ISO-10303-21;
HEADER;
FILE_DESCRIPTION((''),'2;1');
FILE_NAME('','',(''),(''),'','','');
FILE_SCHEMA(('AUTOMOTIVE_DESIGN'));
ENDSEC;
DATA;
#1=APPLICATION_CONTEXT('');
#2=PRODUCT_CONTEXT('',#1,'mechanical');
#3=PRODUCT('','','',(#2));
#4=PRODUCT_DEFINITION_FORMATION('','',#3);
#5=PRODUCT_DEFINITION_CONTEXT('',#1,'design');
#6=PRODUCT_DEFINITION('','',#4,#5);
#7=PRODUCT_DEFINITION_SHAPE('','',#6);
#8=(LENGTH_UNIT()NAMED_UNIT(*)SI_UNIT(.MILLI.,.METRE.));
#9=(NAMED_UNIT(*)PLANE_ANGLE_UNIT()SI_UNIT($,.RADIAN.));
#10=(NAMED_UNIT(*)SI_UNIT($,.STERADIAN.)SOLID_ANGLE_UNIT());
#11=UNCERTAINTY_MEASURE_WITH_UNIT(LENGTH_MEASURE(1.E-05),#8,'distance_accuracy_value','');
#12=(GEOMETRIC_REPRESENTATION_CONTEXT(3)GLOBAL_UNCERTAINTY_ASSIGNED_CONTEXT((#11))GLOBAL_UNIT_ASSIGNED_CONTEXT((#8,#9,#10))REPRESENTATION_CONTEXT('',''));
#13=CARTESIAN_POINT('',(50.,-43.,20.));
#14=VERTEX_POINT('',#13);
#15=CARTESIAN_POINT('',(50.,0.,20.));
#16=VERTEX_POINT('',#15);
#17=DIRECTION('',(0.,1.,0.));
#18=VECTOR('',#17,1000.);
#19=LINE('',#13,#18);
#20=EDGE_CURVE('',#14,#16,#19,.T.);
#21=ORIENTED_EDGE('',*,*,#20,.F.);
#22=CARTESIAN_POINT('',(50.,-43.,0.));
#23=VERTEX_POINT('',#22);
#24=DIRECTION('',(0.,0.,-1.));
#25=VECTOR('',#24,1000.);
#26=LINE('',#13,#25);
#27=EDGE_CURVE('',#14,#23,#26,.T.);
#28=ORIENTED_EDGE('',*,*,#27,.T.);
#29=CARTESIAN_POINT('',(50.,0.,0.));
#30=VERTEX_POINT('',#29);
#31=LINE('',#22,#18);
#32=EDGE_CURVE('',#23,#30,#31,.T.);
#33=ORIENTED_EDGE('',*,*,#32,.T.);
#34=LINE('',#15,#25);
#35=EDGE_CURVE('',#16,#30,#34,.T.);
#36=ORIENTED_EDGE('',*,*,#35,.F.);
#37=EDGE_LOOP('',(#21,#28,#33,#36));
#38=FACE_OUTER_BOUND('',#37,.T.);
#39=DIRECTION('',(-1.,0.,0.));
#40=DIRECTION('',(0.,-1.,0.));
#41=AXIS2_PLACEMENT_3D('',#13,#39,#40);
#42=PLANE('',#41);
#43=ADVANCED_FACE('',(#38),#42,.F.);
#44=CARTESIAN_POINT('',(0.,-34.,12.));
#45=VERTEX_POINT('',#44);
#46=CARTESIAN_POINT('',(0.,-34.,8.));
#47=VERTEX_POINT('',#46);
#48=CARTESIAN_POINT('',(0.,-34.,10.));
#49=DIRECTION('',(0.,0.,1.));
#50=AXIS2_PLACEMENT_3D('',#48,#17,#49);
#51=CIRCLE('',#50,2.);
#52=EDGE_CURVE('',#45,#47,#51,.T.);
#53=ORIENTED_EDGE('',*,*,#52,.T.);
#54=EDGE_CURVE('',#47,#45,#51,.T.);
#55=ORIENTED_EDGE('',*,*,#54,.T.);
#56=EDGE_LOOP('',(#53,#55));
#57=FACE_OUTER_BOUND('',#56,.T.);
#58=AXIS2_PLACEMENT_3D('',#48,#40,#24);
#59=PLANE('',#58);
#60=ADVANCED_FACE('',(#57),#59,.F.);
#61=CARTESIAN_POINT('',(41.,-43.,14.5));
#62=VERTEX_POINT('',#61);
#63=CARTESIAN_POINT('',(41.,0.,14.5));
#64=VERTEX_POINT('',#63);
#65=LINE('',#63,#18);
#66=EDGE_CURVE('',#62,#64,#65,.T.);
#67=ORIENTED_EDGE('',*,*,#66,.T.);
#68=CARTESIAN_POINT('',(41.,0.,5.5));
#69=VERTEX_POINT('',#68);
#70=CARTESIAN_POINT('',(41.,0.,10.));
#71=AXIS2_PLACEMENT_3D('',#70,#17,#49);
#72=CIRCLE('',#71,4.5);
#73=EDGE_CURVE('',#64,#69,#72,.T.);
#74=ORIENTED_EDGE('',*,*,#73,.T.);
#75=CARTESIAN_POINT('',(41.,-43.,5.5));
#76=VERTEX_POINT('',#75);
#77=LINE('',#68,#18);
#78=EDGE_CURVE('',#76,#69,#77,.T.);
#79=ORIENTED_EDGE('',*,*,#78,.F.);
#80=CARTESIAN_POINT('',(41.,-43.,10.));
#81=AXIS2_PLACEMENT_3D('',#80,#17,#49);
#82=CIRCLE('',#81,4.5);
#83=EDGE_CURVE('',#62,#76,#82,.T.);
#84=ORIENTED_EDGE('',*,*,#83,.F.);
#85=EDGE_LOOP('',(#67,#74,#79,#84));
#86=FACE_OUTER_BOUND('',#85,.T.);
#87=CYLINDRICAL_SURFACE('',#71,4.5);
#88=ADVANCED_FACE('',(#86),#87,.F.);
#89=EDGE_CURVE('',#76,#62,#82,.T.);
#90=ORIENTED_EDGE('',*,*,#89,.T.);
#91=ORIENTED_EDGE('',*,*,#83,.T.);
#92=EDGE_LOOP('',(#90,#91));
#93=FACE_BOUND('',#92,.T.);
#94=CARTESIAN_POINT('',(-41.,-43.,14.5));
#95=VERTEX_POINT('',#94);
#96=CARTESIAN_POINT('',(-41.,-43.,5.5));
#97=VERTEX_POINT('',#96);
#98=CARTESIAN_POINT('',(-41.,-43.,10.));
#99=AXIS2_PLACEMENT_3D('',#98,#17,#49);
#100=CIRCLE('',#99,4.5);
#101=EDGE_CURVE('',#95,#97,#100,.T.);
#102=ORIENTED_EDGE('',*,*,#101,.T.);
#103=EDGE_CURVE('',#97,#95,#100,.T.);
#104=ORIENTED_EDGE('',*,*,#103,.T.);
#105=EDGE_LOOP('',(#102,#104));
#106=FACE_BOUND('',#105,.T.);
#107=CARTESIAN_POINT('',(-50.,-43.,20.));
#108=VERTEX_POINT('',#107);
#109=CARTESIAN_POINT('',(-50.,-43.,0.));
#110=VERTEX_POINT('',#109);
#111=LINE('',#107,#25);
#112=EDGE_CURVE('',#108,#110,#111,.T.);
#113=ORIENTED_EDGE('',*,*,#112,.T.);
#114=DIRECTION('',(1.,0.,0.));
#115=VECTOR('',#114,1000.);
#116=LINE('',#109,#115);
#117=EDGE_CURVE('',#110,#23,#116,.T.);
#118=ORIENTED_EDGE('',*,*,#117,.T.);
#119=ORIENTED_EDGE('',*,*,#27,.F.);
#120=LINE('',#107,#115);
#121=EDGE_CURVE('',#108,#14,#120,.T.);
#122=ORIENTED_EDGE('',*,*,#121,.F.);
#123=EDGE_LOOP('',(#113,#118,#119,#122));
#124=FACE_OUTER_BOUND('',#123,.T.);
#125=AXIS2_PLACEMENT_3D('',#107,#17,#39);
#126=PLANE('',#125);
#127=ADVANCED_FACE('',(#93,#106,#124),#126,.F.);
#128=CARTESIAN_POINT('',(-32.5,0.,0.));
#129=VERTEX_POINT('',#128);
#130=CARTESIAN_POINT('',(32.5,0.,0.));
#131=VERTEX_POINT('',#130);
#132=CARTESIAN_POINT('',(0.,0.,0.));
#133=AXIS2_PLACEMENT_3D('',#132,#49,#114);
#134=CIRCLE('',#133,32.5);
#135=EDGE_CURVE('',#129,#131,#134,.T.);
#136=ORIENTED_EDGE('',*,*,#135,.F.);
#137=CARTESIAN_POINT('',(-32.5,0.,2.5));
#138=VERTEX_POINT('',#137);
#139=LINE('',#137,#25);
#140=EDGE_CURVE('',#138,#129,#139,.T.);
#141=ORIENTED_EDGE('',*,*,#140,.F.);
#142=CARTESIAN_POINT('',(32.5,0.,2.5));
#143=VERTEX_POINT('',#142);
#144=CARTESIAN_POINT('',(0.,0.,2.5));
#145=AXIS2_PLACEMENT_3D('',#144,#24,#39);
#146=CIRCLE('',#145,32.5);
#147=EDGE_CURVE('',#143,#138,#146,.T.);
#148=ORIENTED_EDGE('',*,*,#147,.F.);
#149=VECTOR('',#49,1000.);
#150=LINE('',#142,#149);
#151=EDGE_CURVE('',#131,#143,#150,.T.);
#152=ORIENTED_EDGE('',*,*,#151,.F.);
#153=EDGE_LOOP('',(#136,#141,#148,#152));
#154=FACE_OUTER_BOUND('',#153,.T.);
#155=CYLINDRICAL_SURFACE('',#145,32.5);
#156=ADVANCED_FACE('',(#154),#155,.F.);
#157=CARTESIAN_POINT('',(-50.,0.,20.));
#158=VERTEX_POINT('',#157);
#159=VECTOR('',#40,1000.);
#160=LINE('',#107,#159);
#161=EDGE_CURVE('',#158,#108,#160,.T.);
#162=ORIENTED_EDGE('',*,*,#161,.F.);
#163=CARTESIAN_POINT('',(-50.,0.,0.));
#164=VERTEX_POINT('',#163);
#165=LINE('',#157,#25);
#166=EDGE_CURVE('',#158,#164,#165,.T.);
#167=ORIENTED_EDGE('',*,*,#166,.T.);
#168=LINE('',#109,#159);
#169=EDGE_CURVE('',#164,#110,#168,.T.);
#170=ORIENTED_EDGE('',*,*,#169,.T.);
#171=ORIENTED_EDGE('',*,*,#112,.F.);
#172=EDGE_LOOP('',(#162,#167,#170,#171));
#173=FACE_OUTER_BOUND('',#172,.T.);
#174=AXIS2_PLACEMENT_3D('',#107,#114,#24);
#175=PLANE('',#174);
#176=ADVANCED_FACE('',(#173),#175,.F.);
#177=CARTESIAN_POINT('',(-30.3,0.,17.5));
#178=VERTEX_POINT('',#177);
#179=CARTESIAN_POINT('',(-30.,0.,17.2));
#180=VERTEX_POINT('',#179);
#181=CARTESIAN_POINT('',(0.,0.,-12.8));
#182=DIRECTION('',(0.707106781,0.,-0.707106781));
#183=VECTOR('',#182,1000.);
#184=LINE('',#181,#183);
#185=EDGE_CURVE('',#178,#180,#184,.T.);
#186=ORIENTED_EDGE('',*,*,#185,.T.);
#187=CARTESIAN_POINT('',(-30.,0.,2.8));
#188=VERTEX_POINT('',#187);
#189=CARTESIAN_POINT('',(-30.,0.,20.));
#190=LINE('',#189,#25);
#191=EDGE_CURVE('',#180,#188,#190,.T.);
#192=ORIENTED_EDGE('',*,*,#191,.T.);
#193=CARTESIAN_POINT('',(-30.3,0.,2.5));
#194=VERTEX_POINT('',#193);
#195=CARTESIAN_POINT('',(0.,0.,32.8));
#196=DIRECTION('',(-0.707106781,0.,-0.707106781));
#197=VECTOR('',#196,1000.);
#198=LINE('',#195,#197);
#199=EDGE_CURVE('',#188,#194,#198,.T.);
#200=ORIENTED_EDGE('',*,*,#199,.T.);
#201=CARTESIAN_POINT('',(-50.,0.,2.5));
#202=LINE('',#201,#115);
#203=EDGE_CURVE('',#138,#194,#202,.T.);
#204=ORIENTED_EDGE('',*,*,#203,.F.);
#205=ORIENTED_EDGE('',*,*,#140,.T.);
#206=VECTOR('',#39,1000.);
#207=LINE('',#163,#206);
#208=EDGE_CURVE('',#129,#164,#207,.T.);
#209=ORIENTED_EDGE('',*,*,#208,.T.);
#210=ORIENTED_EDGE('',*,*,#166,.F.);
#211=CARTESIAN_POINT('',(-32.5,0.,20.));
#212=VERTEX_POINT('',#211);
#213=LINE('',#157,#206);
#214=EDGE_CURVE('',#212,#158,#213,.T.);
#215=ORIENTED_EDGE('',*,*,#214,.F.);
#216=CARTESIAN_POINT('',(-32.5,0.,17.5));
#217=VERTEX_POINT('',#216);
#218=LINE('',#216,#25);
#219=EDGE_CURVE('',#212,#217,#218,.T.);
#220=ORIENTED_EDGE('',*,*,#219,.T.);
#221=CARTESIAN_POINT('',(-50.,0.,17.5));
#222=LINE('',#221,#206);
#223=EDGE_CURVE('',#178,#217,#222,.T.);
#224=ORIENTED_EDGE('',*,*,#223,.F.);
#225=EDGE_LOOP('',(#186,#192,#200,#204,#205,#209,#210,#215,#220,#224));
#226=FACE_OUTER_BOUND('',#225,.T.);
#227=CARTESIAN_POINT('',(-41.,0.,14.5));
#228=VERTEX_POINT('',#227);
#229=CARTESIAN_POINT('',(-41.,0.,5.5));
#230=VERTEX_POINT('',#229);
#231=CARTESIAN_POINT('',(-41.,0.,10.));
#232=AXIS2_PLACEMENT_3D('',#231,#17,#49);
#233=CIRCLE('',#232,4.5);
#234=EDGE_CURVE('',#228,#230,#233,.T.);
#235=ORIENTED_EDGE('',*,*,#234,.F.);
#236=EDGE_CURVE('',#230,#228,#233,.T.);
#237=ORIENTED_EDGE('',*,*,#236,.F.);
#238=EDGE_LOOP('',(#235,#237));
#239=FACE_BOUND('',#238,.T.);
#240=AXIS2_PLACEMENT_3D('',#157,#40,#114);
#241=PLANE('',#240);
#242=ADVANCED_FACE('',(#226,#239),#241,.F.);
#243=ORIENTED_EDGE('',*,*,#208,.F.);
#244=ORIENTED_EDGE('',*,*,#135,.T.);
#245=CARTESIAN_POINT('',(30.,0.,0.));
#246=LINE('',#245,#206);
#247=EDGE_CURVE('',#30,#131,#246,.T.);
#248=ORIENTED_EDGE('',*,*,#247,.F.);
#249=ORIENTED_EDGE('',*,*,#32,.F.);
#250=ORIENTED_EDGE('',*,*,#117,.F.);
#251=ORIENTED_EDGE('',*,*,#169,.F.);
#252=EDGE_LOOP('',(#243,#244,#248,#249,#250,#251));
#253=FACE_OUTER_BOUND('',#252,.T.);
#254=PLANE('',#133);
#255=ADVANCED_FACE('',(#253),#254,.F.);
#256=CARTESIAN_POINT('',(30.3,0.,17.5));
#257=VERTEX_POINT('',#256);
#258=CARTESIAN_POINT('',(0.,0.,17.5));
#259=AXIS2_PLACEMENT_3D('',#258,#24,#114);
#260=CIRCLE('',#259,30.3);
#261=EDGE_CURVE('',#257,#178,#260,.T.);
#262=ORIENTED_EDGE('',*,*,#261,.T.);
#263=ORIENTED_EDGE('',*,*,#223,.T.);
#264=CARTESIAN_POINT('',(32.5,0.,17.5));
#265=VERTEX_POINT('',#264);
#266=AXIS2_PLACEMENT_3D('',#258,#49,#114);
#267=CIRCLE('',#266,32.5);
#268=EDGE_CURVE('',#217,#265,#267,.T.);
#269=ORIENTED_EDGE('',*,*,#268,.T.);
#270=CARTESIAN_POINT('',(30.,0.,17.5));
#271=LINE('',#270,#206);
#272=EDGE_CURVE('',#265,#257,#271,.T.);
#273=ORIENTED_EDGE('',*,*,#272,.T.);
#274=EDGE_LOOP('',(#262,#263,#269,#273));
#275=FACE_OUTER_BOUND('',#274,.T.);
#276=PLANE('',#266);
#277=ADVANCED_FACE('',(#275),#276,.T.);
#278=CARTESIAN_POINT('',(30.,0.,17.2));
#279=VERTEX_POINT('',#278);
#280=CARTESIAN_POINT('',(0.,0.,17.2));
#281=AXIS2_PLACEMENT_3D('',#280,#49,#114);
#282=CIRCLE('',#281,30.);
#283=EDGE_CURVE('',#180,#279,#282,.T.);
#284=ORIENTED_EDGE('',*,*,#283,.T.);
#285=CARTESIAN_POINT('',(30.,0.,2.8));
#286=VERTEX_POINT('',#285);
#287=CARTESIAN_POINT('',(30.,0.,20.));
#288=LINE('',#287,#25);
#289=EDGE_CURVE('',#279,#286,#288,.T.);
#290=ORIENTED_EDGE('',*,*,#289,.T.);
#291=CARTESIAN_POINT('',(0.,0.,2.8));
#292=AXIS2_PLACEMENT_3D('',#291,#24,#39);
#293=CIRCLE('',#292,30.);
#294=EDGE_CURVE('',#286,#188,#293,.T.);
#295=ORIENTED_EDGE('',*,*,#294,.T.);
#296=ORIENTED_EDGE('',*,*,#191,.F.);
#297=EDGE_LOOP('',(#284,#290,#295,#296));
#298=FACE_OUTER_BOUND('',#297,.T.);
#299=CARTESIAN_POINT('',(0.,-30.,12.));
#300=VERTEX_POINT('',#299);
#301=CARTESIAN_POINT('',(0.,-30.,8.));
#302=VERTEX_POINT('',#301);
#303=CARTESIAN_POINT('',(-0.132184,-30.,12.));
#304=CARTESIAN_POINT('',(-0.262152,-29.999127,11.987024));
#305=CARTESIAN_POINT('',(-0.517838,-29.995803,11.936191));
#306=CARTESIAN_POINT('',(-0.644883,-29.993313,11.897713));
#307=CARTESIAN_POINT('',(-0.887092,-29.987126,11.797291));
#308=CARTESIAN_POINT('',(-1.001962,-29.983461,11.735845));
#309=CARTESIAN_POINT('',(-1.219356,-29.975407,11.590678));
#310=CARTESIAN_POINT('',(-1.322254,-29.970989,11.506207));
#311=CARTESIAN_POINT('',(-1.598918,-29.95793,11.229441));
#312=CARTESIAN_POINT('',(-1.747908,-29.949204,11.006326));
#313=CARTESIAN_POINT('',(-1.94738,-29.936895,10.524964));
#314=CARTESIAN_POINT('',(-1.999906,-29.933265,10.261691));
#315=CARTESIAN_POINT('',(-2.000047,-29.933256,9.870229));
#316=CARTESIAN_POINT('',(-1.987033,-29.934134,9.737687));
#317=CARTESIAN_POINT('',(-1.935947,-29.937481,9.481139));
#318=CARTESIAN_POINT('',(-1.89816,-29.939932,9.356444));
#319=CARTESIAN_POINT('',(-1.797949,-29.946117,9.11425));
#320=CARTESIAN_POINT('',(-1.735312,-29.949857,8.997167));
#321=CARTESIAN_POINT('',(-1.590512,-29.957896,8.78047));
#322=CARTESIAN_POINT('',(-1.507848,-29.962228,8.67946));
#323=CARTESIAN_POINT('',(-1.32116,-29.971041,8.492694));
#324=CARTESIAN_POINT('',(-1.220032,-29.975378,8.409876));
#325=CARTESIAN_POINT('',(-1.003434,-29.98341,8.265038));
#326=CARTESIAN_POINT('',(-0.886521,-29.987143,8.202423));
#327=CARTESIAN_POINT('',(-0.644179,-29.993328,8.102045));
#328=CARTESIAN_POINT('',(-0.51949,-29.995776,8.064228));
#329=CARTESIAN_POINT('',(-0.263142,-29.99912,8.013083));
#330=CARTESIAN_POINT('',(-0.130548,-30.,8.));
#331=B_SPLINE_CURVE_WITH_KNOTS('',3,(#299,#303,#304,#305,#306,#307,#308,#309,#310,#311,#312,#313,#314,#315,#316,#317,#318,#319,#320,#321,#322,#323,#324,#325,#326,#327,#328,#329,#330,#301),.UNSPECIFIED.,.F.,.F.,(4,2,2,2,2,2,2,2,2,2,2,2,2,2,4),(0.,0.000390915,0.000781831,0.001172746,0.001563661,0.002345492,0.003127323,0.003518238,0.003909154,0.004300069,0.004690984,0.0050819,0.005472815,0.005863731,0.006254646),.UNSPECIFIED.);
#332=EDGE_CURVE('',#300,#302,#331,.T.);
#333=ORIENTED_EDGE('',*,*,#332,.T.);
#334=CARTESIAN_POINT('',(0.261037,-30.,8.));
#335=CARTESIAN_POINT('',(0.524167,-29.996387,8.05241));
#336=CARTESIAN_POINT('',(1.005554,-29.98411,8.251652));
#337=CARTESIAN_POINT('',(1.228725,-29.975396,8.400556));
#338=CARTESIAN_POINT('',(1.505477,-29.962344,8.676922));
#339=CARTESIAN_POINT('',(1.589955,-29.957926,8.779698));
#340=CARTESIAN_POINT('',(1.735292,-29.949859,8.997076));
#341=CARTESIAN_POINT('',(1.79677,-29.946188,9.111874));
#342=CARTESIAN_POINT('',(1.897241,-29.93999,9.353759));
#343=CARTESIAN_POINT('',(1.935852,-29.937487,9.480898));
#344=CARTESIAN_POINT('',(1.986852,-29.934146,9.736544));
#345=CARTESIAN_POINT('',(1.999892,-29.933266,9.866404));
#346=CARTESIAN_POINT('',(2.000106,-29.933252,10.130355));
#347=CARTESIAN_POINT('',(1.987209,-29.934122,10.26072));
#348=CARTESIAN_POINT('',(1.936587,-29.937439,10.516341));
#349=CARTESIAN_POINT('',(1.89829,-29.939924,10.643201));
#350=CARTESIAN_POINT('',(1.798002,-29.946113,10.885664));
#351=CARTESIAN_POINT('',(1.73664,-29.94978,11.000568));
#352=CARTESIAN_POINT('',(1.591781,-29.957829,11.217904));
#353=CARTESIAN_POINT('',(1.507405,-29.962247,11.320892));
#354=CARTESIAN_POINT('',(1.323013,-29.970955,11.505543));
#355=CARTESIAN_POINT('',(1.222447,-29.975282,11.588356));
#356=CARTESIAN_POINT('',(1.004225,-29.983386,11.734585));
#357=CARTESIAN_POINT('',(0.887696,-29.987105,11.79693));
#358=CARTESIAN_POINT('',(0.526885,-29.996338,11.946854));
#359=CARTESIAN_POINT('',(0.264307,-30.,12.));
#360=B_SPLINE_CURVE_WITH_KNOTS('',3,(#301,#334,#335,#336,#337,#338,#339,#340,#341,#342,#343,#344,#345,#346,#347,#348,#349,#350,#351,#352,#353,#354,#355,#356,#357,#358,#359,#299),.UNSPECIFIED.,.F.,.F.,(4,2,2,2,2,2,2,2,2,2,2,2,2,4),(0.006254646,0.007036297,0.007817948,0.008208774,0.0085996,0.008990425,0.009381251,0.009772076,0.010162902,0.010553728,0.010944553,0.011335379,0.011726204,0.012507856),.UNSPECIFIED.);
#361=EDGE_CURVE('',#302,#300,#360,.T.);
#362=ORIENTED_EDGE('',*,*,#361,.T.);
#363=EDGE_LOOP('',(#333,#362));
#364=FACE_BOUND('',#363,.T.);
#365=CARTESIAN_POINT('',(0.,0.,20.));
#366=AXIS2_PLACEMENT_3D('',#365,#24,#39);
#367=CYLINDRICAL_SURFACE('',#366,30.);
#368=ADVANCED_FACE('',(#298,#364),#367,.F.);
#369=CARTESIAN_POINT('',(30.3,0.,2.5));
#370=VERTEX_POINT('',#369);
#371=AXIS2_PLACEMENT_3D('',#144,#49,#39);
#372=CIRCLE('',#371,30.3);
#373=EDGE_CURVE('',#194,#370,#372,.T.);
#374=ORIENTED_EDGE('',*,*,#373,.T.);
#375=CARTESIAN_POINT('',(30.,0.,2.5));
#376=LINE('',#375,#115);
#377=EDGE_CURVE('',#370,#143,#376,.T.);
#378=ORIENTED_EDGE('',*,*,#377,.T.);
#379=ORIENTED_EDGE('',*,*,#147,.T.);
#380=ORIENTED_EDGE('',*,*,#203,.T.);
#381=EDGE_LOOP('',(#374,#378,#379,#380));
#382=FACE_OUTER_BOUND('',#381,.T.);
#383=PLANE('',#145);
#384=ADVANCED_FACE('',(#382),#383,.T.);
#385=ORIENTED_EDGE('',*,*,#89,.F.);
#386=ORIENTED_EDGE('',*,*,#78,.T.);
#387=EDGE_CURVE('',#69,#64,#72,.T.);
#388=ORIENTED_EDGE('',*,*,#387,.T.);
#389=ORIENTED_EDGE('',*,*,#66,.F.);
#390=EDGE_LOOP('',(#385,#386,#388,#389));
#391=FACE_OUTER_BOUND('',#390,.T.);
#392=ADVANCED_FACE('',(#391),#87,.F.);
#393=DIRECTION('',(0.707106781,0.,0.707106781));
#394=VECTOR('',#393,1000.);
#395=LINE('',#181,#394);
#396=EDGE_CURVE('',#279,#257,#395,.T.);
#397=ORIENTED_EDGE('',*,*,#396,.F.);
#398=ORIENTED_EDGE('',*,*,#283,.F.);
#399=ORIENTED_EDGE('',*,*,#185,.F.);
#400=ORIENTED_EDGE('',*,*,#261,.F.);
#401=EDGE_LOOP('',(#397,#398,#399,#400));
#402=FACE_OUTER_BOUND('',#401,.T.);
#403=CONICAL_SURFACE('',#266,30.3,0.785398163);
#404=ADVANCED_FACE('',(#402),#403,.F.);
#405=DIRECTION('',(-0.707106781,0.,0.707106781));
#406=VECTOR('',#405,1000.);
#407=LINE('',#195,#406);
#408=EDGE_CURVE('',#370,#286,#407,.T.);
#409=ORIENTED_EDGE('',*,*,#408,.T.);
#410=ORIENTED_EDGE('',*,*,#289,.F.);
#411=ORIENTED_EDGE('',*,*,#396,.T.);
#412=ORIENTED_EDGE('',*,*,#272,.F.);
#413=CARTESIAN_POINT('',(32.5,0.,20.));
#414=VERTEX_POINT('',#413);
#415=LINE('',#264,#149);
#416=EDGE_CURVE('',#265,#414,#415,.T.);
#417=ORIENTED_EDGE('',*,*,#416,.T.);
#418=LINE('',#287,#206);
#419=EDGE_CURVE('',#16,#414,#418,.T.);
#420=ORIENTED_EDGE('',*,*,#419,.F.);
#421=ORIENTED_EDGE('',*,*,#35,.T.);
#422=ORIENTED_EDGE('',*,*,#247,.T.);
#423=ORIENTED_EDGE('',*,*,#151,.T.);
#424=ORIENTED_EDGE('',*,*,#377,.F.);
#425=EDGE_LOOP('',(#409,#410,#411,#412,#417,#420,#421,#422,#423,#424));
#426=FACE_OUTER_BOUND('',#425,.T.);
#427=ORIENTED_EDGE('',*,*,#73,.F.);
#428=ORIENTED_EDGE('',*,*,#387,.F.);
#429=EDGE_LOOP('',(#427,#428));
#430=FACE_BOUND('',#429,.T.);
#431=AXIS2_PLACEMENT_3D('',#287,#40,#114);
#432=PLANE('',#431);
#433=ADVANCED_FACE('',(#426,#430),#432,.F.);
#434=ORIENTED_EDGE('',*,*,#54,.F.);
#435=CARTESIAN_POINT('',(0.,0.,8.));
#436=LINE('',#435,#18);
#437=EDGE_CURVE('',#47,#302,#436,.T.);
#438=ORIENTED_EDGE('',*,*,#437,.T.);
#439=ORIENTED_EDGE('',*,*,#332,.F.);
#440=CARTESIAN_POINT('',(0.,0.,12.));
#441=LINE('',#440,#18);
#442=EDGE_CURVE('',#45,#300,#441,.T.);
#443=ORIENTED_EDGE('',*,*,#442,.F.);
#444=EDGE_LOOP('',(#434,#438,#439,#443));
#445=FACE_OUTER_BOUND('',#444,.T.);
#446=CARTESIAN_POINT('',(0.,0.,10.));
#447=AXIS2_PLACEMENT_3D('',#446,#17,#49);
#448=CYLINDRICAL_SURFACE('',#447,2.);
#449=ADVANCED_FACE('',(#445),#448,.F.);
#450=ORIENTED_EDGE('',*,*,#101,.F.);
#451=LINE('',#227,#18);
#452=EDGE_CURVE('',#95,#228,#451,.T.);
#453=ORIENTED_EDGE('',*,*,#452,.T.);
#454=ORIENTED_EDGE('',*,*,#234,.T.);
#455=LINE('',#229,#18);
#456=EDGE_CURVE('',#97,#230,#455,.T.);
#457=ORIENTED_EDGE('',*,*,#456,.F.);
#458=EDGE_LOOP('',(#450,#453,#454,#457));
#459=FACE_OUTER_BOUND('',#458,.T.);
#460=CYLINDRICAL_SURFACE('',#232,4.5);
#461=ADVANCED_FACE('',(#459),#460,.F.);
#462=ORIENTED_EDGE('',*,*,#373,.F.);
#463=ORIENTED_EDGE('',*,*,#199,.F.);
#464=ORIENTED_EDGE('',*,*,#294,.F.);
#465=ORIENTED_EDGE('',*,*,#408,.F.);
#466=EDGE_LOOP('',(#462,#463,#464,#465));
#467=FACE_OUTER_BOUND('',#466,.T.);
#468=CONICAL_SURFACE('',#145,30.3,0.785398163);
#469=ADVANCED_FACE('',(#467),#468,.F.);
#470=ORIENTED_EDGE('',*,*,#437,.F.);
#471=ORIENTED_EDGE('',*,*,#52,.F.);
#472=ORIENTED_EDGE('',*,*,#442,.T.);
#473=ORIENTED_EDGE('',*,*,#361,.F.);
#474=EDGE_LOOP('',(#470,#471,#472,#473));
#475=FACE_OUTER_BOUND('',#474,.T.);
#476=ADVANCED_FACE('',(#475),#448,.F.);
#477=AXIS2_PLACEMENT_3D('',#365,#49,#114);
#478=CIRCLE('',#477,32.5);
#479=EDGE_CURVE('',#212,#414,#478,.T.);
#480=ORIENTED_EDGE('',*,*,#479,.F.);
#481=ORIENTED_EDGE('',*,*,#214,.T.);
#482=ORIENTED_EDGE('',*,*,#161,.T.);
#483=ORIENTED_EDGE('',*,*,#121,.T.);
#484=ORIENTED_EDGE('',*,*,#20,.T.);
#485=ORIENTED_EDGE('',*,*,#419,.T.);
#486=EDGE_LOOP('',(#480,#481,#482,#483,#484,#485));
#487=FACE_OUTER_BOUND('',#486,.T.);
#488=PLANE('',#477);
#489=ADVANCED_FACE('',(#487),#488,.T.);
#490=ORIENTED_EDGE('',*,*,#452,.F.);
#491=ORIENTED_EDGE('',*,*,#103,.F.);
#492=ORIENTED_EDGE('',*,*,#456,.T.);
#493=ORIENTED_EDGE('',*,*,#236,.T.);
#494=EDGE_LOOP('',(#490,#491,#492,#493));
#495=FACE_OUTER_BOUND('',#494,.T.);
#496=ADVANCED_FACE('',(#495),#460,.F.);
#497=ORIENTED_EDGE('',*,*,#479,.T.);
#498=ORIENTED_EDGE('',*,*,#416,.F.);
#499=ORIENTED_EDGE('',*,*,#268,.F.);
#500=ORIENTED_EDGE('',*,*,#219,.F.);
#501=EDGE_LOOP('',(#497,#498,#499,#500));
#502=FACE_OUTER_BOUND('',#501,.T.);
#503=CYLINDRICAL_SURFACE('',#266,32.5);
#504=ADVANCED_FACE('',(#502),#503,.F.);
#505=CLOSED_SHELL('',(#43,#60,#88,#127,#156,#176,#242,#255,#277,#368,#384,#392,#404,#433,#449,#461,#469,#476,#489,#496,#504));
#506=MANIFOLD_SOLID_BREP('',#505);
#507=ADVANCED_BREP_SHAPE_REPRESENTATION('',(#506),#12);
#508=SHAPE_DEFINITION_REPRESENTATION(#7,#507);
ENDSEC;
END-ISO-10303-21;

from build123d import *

# Parameters (mm, degrees)
BOSS_EXTRUDE1_DEPTH = 20
SKETCH2_R           = 32.5
CUT_EXTRUDE1_DEPTH  = 2.5
CUT_EXTRUDE2_START  = -2.5
SKETCH3_R           = 32.5
CUT_EXTRUDE2_DEPTH  = 2.5
CHAMFER1_SIZE       = 0.3
HOLE1_D             = 9
HOLE2_D             = 4
HOLE2_DEPTH         = 34


with BuildPart() as part:
    # Sketch1 → Boss-Extrude1 (new body)
    with BuildSketch(Plane.XY):
        with BuildLine():
            Line((-50, 0), (-30, 0))
            ThreePointArc((-30, 0), (0, -30), (30, 0))
            Line((30, 0), (50, 0))
            Line((50, 0), (50, -43))
            Line((50, -43), (-50, -43))
            Line((-50, -43), (-50, 0))
        make_face()
    extrude(amount=BOSS_EXTRUDE1_DEPTH)

    # Sketch2 → Cut-Extrude1 (cut)
    with BuildSketch(Plane.XY.offset(20)):
        Circle(SKETCH2_R)
    extrude(amount=-CUT_EXTRUDE1_DEPTH, mode=Mode.SUBTRACT)

    # Sketch3 → Cut-Extrude2 (cut)
    with BuildSketch(Plane(origin=(0, 0, 0), x_dir=(-1, 0, 0), z_dir=(0, 0, -1)).offset(CUT_EXTRUDE2_START)):
        Circle(SKETCH3_R)
    extrude(amount=CUT_EXTRUDE2_DEPTH, mode=Mode.SUBTRACT)

    # Chamfer1
    chamfer1_edges = [part.edges().sort_by_distance(p)[0] for p in [
        (0, -30, 17.5),
        (0, -30, 2.5),
    ]]
    chamfer(chamfer1_edges, length=CHAMFER1_SIZE)

    # Hole1 (through all)
    with Locations(Plane(origin=(0, 0, 0), x_dir=(1, 0, 0), z_dir=(0, 1, 0))):
        with Locations((-41, -10), (41, -10)):
            Hole(HOLE1_D / 2)

    # Hole2
    with Locations(Plane(origin=(0, 0, 0), x_dir=(1, 0, 0), z_dir=(0, 1, 0))):
        with Locations((0, -10)):
            Hole(HOLE2_D / 2, depth=HOLE2_DEPTH)


solid = part.part
